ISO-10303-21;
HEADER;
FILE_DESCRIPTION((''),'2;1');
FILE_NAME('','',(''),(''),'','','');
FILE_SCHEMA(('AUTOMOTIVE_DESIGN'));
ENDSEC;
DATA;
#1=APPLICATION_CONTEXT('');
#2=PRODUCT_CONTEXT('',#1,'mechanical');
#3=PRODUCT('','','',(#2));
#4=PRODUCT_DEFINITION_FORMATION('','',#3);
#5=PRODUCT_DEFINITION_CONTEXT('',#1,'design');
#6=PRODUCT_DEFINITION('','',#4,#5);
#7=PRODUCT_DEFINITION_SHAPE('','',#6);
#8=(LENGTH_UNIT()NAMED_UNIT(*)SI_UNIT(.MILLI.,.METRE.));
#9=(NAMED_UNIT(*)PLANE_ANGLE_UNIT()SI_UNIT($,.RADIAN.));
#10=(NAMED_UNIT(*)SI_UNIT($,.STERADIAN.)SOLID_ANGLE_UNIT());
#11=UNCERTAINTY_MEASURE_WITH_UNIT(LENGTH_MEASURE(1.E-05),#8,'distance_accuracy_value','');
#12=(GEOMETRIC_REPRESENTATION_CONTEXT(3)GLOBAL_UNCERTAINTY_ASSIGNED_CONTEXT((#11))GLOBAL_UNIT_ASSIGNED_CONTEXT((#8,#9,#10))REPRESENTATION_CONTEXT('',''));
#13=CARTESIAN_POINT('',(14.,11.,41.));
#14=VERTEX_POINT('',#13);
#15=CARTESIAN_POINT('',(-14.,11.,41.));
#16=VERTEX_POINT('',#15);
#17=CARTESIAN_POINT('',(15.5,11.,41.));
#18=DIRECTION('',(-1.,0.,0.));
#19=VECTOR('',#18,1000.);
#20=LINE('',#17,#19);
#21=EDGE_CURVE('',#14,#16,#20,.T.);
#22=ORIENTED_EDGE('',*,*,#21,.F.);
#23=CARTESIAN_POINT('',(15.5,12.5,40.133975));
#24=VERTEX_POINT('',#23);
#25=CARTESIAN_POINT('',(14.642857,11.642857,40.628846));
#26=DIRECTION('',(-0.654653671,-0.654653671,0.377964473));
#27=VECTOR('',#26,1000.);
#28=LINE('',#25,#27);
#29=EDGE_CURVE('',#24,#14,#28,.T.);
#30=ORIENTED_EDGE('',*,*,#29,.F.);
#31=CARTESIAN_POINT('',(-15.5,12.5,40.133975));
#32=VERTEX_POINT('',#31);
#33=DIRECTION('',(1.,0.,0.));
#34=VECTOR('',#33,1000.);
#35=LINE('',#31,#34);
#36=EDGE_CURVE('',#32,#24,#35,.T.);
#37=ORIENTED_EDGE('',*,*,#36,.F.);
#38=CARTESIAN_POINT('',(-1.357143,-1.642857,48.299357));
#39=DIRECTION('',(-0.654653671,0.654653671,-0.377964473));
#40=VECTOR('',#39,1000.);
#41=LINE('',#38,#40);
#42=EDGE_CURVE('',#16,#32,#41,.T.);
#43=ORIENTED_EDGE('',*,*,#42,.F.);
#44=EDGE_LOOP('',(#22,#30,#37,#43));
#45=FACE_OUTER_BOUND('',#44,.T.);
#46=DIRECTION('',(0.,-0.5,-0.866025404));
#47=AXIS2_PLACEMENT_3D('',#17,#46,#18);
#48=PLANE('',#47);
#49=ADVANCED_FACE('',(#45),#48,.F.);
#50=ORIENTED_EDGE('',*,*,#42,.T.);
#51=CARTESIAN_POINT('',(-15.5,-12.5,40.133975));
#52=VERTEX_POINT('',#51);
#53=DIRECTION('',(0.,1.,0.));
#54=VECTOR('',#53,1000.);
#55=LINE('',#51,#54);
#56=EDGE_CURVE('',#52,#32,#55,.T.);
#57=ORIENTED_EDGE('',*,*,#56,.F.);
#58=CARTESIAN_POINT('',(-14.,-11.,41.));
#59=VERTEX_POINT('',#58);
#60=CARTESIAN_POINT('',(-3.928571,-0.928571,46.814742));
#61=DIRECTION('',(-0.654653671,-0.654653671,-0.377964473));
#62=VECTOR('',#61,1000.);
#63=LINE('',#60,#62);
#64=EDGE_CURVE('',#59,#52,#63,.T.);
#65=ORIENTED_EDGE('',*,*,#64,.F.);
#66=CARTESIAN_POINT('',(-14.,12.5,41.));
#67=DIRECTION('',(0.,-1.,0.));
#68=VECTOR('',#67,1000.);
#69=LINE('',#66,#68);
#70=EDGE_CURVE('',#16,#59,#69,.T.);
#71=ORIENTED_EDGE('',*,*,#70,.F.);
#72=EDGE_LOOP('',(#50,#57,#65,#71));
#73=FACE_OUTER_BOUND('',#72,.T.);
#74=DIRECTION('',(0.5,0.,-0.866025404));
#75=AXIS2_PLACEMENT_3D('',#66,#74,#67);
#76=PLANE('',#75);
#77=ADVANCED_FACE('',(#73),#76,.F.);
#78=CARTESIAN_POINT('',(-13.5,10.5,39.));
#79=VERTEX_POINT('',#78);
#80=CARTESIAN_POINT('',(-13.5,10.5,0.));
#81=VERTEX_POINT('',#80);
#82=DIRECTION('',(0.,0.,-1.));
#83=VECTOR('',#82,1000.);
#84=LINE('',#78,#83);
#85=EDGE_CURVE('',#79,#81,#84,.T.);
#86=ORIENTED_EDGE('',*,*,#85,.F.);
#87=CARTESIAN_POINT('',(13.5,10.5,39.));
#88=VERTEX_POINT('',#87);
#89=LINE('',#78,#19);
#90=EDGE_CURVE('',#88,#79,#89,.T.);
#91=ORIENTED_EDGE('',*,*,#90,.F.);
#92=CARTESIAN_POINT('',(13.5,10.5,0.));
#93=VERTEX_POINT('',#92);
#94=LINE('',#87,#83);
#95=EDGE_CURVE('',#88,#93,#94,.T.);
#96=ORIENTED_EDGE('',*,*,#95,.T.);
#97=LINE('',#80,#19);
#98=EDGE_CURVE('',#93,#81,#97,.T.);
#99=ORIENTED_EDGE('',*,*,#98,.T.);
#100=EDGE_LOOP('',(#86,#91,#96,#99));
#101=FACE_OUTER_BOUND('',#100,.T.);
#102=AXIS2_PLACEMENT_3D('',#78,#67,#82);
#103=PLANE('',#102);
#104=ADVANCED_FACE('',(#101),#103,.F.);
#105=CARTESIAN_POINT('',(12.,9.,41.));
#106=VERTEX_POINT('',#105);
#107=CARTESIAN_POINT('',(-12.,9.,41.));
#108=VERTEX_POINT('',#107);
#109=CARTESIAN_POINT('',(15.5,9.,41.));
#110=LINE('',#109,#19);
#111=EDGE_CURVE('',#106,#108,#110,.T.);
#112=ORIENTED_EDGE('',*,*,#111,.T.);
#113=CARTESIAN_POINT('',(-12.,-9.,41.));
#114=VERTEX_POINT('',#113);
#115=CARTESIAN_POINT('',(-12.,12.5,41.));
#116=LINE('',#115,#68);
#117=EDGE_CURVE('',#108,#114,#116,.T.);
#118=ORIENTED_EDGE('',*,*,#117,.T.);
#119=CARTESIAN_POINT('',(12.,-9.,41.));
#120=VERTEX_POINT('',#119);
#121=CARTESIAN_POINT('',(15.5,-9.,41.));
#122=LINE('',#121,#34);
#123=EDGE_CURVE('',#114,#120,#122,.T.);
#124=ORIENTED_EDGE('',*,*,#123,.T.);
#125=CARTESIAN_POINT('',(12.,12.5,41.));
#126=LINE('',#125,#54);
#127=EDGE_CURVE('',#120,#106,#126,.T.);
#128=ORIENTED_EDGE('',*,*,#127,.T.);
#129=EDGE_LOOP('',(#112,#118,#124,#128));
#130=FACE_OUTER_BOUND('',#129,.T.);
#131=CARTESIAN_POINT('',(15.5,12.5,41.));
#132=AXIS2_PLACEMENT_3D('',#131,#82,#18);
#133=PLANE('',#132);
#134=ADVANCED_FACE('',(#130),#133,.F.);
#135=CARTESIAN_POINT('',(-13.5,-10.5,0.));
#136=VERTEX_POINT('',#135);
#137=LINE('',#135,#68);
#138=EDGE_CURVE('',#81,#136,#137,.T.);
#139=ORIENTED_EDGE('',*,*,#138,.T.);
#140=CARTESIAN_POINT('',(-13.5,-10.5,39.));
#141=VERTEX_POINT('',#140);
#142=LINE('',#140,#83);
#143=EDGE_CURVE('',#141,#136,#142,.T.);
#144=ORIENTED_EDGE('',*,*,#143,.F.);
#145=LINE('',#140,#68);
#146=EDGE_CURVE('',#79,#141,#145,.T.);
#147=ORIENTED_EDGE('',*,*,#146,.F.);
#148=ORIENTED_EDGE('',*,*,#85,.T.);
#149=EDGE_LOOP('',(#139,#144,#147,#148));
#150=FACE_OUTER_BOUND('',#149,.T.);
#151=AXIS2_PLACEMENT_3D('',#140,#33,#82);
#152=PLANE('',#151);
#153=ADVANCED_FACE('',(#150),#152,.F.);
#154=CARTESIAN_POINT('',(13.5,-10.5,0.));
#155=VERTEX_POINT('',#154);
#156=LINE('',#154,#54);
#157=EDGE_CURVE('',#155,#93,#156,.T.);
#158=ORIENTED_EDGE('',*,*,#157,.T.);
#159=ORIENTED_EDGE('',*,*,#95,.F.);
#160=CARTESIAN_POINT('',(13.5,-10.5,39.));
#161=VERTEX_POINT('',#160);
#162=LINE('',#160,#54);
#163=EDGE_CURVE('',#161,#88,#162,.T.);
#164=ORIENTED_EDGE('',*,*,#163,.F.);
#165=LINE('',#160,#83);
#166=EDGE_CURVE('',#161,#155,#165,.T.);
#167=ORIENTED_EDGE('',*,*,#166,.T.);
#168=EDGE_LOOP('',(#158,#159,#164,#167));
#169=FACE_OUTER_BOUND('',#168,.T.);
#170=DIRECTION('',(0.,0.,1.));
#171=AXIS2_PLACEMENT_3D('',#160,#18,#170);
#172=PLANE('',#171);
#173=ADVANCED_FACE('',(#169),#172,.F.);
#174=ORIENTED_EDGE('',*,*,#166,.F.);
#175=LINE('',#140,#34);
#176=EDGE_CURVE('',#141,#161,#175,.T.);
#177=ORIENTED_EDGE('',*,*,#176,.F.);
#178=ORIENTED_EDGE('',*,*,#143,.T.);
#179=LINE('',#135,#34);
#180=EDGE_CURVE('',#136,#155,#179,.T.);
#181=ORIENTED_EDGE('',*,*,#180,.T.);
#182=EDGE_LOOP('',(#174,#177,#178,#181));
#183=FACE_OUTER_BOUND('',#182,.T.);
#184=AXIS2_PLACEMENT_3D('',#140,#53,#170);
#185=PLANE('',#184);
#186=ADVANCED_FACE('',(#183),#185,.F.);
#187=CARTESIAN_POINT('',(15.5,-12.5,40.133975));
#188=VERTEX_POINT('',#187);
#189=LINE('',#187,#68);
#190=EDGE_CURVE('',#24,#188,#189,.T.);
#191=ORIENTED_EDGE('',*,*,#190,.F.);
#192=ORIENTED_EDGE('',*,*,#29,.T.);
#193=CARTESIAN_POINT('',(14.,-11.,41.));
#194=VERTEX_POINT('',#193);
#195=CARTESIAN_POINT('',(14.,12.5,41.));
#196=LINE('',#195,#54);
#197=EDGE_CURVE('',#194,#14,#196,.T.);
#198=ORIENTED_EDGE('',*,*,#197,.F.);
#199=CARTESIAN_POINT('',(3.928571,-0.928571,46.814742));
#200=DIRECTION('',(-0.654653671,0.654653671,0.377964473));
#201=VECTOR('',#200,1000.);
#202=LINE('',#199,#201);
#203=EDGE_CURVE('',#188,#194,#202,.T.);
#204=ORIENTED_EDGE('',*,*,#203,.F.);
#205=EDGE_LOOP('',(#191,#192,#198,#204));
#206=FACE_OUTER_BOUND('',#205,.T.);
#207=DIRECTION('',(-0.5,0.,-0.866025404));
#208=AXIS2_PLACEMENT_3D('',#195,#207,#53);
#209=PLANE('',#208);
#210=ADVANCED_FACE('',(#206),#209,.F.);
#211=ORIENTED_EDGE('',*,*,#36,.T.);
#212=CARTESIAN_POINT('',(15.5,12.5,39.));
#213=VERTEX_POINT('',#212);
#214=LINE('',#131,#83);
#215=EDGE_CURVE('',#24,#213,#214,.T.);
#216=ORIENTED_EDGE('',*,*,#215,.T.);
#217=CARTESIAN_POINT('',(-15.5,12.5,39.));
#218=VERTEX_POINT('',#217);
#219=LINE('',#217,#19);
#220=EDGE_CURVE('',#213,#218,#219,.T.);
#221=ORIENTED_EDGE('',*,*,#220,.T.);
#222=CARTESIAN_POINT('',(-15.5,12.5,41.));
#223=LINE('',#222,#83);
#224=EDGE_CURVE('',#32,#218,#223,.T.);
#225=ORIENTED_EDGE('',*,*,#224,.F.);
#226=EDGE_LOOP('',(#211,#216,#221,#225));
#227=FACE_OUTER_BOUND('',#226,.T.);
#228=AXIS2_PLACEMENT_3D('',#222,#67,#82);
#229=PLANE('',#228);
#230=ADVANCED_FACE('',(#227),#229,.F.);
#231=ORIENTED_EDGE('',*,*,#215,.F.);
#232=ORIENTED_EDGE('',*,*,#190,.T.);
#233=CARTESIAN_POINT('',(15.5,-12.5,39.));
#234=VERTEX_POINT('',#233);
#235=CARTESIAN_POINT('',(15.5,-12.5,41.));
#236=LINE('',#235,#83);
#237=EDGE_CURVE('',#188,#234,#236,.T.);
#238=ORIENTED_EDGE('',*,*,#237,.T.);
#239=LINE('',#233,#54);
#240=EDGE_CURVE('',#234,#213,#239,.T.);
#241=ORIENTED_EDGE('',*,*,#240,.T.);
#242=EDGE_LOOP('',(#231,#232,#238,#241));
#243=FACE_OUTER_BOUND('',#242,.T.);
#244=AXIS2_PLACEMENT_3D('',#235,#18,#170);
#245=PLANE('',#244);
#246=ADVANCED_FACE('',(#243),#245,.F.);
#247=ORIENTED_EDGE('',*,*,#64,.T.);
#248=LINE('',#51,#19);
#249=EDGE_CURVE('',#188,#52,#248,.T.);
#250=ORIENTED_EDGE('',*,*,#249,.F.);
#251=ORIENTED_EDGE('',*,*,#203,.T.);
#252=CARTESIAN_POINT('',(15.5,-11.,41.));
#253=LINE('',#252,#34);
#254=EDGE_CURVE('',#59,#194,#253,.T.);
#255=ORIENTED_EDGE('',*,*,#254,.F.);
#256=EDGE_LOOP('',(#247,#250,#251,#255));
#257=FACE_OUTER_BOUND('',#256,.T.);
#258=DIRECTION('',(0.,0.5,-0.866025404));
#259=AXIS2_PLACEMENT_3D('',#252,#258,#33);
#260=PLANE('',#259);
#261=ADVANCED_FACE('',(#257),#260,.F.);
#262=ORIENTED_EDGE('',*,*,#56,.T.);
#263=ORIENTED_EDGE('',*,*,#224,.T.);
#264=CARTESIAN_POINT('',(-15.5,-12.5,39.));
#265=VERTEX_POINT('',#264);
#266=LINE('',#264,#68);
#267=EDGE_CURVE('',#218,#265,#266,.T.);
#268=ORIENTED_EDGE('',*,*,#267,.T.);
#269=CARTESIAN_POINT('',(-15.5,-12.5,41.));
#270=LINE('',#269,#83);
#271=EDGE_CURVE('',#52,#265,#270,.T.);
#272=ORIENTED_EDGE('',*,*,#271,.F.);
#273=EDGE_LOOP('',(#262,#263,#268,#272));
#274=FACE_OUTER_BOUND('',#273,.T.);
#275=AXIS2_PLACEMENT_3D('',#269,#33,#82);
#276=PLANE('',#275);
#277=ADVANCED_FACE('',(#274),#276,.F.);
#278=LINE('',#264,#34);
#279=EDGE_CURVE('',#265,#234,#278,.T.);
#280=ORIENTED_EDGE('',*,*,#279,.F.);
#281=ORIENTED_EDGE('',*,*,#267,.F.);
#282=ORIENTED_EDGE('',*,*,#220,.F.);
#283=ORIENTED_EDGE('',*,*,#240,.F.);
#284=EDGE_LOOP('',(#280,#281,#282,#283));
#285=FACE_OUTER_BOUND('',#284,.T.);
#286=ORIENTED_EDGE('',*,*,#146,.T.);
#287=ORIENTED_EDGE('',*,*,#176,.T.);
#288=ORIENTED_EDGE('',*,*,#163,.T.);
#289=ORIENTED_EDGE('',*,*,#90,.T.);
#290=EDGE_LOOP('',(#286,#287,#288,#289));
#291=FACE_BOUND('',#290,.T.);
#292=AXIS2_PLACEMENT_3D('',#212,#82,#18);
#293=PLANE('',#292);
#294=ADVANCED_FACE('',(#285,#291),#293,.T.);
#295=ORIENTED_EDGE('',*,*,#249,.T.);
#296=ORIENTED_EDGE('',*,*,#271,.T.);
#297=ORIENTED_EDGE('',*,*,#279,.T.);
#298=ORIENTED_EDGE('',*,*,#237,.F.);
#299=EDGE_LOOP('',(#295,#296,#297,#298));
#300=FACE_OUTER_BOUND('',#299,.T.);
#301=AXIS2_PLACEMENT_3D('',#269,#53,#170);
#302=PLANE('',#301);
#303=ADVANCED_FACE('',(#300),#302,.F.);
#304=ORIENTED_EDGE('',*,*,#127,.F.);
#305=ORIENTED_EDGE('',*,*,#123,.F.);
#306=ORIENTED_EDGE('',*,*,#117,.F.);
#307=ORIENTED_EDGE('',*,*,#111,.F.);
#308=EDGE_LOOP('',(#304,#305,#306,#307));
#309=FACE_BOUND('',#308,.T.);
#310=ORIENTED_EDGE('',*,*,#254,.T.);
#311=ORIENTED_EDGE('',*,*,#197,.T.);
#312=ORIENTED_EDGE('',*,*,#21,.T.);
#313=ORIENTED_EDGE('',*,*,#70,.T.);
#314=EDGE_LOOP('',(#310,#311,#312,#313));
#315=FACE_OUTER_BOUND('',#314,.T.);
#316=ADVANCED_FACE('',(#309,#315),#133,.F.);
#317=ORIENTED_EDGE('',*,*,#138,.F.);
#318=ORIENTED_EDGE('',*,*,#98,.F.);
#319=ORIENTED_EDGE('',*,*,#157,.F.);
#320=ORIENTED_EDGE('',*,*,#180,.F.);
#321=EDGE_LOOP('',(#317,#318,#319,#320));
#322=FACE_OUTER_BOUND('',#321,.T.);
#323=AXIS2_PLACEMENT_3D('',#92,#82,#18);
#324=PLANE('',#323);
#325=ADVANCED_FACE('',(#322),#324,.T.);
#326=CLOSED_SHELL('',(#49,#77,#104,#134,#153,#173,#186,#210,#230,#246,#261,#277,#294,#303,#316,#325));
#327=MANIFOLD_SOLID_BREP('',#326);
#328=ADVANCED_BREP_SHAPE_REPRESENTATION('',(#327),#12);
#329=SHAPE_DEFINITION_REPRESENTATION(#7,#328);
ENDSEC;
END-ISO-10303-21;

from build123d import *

# Parameters (mm, degrees)
SKETCH1_W           = 27
SKETCH1_H           = 21
BOSS_EXTRUDE1_DEPTH = 39
SKETCH2_W           = 31
SKETCH2_H           = 25
BOSS_EXTRUDE2_DEPTH = 2
CHAMFER1_SIZE       = 1.5
CHAMFER1_SIZE2      = 0.866025404


with BuildPart() as part:
    # Sketch1 → Boss-Extrude1 (new body)
    with BuildSketch(Plane.XY):
        Rectangle(SKETCH1_W, SKETCH1_H)
    extrude(amount=BOSS_EXTRUDE1_DEPTH)

    # Sketch2 → Boss-Extrude2 (add)
    with BuildSketch(Plane.XY.offset(39)):
        Rectangle(SKETCH2_W, SKETCH2_H)
    extrude(amount=BOSS_EXTRUDE2_DEPTH)

    # Chamfer1
    chamfer1_edges = [part.edges().sort_by_distance(p)[0] for p in [
        (15.5, 0, 41),
        (0, 12.5, 41),
        (-15.5, 0, 41),
        (0, -12.5, 41),
    ]]
    chamfer1_side = [part.faces().sort_by_distance(p)[0] for p in [
        (0, 0, 41),
    ]]
    chamfer(chamfer1_edges, length=CHAMFER1_SIZE, length2=CHAMFER1_SIZE2, reference=chamfer1_side[0])


solid = part.part
